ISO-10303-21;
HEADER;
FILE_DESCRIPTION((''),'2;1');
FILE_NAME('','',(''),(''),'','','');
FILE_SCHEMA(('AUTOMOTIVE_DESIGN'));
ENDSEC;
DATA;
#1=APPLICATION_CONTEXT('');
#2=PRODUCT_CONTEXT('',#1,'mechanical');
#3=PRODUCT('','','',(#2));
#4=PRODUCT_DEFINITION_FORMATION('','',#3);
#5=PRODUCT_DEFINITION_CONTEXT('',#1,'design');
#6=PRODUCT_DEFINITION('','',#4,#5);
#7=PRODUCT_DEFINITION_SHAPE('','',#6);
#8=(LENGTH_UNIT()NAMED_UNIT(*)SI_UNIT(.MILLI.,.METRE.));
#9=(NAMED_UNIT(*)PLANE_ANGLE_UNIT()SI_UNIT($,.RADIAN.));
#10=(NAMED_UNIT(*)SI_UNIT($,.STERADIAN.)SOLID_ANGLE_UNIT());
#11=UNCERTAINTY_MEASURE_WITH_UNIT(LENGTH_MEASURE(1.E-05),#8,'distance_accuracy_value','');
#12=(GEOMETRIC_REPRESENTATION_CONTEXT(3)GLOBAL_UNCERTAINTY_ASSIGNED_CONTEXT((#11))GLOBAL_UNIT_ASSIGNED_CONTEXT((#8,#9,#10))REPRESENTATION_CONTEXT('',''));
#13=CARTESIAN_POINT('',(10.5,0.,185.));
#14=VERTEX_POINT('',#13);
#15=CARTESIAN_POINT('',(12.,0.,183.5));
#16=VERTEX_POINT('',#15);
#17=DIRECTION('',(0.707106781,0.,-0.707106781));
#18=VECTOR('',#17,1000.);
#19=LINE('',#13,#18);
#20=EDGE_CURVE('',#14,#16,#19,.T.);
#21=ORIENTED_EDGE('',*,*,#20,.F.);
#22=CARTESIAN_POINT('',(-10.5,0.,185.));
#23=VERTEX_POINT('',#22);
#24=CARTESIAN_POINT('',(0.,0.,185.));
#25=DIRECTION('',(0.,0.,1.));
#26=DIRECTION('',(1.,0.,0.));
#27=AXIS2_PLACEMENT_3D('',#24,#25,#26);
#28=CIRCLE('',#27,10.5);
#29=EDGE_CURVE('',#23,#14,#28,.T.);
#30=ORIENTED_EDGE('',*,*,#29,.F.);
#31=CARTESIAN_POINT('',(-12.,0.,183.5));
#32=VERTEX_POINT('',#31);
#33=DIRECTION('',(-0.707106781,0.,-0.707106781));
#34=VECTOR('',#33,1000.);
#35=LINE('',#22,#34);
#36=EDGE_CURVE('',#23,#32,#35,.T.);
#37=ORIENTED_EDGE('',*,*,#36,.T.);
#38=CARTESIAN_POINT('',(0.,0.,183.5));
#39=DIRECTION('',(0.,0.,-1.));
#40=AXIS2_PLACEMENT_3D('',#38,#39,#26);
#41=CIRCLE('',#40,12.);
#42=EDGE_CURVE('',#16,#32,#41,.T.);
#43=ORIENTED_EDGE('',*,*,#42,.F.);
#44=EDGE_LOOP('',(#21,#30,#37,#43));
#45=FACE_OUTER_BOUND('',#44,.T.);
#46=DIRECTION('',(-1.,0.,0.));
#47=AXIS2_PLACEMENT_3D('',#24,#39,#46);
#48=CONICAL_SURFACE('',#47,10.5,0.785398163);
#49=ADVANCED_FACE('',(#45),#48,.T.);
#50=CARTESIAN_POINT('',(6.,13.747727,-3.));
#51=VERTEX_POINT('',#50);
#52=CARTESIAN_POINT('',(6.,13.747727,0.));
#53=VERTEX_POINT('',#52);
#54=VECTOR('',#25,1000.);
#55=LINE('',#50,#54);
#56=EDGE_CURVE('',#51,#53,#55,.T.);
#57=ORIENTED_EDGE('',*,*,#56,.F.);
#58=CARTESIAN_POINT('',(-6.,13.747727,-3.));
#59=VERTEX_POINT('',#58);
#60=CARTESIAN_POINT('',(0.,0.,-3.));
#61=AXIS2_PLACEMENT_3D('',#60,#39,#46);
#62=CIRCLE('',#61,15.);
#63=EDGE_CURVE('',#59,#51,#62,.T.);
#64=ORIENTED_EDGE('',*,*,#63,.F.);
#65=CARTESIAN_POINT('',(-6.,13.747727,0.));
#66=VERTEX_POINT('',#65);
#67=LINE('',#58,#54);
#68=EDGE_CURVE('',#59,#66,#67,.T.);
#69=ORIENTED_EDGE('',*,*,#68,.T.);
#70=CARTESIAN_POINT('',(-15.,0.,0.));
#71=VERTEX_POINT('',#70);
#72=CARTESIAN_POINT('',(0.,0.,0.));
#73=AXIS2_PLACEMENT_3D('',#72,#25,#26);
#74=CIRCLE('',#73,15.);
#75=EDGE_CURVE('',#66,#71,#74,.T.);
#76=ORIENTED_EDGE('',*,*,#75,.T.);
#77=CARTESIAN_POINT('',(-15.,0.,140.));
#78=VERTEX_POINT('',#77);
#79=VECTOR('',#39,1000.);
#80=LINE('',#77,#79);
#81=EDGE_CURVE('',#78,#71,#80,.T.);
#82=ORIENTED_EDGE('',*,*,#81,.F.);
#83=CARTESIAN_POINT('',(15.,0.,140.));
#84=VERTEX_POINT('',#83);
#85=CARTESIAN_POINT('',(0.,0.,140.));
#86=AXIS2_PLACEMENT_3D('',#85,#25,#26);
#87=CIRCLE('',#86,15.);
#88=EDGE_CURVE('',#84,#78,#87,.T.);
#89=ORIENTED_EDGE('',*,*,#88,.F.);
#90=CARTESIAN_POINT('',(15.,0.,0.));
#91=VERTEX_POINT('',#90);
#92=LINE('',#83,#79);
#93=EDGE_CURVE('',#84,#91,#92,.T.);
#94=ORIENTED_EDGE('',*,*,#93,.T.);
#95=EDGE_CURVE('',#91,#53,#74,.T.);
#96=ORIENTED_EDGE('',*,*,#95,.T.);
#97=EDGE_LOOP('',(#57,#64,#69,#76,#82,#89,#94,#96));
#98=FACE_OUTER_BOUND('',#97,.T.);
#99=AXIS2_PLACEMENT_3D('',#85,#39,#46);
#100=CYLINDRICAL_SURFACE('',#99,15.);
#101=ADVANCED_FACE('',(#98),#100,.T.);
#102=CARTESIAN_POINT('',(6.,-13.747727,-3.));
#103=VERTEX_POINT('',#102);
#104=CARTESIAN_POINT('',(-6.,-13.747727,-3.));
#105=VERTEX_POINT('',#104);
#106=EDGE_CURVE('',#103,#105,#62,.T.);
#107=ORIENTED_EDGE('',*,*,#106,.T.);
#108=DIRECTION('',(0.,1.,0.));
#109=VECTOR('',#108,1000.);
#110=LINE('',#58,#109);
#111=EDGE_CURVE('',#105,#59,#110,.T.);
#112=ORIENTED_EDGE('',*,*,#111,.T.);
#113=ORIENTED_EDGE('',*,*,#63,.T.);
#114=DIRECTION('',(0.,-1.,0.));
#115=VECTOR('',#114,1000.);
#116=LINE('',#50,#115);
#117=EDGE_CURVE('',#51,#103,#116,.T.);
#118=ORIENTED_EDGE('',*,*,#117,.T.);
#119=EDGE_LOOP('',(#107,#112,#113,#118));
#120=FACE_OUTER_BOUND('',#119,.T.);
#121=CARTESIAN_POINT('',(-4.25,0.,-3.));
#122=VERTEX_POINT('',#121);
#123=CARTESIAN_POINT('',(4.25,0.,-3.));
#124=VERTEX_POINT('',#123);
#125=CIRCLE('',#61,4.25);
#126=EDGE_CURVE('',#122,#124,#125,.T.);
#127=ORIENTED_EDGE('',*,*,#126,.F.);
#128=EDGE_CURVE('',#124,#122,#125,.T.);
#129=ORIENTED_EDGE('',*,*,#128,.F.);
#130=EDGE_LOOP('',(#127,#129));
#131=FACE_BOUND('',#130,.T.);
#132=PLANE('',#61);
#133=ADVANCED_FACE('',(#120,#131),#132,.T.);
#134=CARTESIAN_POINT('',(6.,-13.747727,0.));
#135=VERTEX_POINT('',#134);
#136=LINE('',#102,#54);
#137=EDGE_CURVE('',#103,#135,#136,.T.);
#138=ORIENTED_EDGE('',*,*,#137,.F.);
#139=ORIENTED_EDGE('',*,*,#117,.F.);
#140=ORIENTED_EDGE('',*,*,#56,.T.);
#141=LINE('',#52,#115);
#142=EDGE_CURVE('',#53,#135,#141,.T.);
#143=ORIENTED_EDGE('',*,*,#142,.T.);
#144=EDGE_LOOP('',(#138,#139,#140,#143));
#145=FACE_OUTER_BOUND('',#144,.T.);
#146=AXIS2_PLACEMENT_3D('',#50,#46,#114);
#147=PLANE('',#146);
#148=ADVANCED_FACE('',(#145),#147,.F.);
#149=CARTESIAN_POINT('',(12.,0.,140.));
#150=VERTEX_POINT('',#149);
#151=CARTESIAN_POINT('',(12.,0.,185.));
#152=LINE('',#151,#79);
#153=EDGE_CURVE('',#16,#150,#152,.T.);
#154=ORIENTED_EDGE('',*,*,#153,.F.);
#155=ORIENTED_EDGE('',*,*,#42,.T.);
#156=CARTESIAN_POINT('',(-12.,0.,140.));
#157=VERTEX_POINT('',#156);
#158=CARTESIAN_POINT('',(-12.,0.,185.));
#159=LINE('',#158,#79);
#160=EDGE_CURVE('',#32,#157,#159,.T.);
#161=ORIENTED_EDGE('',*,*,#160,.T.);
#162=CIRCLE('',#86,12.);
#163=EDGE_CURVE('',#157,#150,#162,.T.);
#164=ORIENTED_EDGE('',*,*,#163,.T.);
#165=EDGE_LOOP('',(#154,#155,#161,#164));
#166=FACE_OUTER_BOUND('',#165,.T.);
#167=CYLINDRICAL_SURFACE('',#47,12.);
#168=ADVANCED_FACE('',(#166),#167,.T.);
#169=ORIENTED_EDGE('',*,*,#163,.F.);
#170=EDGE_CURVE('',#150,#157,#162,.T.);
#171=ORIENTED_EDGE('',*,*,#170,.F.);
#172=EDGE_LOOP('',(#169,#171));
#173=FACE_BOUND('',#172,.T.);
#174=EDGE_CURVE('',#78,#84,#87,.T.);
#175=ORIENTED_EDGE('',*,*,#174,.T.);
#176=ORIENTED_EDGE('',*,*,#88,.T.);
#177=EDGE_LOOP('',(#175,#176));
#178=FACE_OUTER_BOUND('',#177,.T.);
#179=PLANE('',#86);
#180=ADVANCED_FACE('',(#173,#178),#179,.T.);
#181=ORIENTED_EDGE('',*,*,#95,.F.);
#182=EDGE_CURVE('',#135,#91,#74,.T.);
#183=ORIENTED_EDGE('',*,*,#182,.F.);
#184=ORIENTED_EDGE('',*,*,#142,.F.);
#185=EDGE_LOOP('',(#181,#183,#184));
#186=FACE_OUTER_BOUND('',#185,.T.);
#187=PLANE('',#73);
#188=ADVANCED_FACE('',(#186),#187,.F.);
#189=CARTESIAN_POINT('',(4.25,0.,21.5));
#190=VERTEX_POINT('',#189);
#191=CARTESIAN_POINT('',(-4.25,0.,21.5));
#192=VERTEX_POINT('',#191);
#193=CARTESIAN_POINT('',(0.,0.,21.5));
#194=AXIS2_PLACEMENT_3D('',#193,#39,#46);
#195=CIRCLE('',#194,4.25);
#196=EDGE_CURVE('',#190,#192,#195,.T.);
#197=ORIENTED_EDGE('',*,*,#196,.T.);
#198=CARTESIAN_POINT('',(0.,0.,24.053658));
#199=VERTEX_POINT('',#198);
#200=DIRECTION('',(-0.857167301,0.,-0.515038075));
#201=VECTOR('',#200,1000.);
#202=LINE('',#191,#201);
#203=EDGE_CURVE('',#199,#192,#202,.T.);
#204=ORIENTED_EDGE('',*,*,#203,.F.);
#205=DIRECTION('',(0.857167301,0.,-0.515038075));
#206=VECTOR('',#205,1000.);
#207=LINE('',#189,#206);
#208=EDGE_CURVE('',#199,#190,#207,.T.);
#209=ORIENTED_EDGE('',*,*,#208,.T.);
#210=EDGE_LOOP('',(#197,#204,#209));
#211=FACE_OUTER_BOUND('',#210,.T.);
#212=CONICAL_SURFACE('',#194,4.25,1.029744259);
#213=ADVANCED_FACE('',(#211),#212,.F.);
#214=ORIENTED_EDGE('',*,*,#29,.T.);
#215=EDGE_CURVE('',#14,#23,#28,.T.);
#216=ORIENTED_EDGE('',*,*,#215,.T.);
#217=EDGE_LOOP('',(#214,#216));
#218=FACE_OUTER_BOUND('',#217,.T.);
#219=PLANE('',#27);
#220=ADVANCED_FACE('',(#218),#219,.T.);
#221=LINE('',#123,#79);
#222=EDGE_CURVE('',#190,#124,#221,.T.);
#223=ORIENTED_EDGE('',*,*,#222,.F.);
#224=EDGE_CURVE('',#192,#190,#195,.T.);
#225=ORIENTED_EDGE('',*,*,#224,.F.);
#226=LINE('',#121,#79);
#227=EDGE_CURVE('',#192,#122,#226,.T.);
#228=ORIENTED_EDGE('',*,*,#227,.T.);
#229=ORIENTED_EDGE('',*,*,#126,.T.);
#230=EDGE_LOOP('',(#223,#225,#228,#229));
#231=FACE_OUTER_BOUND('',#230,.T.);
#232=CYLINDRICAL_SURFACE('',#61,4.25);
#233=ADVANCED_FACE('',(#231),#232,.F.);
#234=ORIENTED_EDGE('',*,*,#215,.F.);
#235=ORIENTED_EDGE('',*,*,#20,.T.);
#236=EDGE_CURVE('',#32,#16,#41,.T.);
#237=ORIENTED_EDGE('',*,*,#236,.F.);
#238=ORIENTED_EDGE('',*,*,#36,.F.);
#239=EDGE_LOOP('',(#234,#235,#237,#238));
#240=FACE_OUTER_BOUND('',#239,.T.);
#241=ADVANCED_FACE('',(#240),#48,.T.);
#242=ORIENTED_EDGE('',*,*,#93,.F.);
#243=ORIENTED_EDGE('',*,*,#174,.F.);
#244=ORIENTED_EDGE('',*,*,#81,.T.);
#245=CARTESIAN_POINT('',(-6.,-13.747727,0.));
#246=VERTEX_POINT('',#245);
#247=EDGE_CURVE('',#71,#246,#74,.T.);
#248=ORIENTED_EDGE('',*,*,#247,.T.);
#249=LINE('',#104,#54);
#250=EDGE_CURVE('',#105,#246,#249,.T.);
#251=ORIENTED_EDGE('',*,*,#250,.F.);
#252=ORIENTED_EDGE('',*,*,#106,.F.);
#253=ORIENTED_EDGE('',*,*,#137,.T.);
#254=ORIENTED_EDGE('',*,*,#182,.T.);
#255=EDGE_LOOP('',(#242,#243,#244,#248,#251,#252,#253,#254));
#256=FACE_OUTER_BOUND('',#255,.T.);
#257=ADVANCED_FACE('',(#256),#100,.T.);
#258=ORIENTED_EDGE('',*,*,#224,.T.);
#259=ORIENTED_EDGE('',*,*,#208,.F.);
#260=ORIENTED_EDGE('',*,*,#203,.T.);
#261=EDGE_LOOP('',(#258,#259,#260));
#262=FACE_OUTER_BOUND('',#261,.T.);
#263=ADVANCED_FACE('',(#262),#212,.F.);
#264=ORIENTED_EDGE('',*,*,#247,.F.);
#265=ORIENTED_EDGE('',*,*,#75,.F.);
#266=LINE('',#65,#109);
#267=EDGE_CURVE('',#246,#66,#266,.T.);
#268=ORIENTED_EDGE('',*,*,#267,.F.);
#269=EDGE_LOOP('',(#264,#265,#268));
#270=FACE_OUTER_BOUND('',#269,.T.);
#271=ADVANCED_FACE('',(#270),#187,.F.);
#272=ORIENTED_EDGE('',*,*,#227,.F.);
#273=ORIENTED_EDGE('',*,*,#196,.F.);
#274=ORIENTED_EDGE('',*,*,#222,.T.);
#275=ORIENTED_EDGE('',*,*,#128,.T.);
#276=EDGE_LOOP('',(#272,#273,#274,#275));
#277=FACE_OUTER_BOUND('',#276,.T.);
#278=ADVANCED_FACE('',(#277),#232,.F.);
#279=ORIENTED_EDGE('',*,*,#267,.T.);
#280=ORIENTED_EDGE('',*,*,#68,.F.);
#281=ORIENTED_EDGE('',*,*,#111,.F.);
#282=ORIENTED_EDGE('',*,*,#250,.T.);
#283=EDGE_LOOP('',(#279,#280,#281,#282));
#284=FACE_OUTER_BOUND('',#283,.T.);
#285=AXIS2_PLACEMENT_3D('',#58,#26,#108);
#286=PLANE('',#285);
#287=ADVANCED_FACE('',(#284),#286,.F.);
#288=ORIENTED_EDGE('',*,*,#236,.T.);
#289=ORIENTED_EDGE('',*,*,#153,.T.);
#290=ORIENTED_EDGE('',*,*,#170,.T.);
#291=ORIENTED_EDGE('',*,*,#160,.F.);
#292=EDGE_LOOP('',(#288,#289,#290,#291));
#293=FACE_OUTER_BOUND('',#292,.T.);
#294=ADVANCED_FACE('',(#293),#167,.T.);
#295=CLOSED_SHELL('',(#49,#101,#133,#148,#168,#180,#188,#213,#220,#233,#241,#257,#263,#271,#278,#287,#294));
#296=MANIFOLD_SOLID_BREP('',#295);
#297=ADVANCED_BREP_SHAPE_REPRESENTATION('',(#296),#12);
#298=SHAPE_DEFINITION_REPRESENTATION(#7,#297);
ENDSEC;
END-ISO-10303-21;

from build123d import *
from build123d.topology import SkipClean

# Parameters (mm, degrees)
SKETCH1_R              = 15
BOSS_EXTRUDE1_DEPTH    = 140
SKETCH2_R              = 12
BOSS_EXTRUDE2_DEPTH    = 45
BOSS_EXTRUDE3_START    = 3
BOSS_EXTRUDE3_DEPTH    = 3
M10_TAPPED_HOLE1_D     = 8.5
M10_TAPPED_HOLE1_DEPTH = 24.5
M10_TAPPED_HOLE1_TIP   = 2.553657631
CHAMFER1_SIZE          = 1.5


with BuildPart() as part:
    # Sketch1 → Boss-Extrude1 (new body)
    with BuildSketch(Plane.XY):
        Circle(SKETCH1_R)
    extrude(amount=BOSS_EXTRUDE1_DEPTH)

    # Sketch2 → Boss-Extrude2 (add)
    with BuildSketch(Plane.XY.offset(140)):
        with Locations(Location((0, 0, 0), (0, 0, 180))):
            Circle(SKETCH2_R)
    extrude(amount=BOSS_EXTRUDE2_DEPTH)

    # Sketch3 → Boss-Extrude3 (add)
    with SkipClean():  # the faces are left unmerged after this step: merging them gives an invalid solid
        with BuildSketch(Plane(origin=(0, 0, 0), x_dir=(-1, 0, 0), z_dir=(0, 0, -1)).offset(BOSS_EXTRUDE3_START)):
            with BuildLine():
                Line((-6, 13.747727085), (-6, -13.747727085))
                ThreePointArc((-6, -13.747727085), (0, -15), (6, -13.747727085))
                Line((6, -13.747727085), (6, 13.747727085))
                ThreePointArc((6, 13.747727085), (0, 15), (-6, 13.747727085))
            make_face()
        extrude(amount=-BOSS_EXTRUDE3_DEPTH)

    # M10 Tapped Hole1
    with Locations(Plane(origin=(0, 0, -3), x_dir=(-1, 0, 0), z_dir=(0, 0, -1))):
        with Locations((0, 0)):
            Hole(M10_TAPPED_HOLE1_D / 2, depth=M10_TAPPED_HOLE1_DEPTH)
            with Locations((0, 0, -(M10_TAPPED_HOLE1_DEPTH + M10_TAPPED_HOLE1_TIP / 2))):  # 118° drill point
                Cone(0, M10_TAPPED_HOLE1_D / 2, M10_TAPPED_HOLE1_TIP, mode=Mode.SUBTRACT)

    # Chamfer1
    chamfer1_edges = [part.edges().sort_by_distance(p)[0] for p in [
        (12, 0, 185),
    ]]
    chamfer(chamfer1_edges, length=CHAMFER1_SIZE)


solid = part.part
